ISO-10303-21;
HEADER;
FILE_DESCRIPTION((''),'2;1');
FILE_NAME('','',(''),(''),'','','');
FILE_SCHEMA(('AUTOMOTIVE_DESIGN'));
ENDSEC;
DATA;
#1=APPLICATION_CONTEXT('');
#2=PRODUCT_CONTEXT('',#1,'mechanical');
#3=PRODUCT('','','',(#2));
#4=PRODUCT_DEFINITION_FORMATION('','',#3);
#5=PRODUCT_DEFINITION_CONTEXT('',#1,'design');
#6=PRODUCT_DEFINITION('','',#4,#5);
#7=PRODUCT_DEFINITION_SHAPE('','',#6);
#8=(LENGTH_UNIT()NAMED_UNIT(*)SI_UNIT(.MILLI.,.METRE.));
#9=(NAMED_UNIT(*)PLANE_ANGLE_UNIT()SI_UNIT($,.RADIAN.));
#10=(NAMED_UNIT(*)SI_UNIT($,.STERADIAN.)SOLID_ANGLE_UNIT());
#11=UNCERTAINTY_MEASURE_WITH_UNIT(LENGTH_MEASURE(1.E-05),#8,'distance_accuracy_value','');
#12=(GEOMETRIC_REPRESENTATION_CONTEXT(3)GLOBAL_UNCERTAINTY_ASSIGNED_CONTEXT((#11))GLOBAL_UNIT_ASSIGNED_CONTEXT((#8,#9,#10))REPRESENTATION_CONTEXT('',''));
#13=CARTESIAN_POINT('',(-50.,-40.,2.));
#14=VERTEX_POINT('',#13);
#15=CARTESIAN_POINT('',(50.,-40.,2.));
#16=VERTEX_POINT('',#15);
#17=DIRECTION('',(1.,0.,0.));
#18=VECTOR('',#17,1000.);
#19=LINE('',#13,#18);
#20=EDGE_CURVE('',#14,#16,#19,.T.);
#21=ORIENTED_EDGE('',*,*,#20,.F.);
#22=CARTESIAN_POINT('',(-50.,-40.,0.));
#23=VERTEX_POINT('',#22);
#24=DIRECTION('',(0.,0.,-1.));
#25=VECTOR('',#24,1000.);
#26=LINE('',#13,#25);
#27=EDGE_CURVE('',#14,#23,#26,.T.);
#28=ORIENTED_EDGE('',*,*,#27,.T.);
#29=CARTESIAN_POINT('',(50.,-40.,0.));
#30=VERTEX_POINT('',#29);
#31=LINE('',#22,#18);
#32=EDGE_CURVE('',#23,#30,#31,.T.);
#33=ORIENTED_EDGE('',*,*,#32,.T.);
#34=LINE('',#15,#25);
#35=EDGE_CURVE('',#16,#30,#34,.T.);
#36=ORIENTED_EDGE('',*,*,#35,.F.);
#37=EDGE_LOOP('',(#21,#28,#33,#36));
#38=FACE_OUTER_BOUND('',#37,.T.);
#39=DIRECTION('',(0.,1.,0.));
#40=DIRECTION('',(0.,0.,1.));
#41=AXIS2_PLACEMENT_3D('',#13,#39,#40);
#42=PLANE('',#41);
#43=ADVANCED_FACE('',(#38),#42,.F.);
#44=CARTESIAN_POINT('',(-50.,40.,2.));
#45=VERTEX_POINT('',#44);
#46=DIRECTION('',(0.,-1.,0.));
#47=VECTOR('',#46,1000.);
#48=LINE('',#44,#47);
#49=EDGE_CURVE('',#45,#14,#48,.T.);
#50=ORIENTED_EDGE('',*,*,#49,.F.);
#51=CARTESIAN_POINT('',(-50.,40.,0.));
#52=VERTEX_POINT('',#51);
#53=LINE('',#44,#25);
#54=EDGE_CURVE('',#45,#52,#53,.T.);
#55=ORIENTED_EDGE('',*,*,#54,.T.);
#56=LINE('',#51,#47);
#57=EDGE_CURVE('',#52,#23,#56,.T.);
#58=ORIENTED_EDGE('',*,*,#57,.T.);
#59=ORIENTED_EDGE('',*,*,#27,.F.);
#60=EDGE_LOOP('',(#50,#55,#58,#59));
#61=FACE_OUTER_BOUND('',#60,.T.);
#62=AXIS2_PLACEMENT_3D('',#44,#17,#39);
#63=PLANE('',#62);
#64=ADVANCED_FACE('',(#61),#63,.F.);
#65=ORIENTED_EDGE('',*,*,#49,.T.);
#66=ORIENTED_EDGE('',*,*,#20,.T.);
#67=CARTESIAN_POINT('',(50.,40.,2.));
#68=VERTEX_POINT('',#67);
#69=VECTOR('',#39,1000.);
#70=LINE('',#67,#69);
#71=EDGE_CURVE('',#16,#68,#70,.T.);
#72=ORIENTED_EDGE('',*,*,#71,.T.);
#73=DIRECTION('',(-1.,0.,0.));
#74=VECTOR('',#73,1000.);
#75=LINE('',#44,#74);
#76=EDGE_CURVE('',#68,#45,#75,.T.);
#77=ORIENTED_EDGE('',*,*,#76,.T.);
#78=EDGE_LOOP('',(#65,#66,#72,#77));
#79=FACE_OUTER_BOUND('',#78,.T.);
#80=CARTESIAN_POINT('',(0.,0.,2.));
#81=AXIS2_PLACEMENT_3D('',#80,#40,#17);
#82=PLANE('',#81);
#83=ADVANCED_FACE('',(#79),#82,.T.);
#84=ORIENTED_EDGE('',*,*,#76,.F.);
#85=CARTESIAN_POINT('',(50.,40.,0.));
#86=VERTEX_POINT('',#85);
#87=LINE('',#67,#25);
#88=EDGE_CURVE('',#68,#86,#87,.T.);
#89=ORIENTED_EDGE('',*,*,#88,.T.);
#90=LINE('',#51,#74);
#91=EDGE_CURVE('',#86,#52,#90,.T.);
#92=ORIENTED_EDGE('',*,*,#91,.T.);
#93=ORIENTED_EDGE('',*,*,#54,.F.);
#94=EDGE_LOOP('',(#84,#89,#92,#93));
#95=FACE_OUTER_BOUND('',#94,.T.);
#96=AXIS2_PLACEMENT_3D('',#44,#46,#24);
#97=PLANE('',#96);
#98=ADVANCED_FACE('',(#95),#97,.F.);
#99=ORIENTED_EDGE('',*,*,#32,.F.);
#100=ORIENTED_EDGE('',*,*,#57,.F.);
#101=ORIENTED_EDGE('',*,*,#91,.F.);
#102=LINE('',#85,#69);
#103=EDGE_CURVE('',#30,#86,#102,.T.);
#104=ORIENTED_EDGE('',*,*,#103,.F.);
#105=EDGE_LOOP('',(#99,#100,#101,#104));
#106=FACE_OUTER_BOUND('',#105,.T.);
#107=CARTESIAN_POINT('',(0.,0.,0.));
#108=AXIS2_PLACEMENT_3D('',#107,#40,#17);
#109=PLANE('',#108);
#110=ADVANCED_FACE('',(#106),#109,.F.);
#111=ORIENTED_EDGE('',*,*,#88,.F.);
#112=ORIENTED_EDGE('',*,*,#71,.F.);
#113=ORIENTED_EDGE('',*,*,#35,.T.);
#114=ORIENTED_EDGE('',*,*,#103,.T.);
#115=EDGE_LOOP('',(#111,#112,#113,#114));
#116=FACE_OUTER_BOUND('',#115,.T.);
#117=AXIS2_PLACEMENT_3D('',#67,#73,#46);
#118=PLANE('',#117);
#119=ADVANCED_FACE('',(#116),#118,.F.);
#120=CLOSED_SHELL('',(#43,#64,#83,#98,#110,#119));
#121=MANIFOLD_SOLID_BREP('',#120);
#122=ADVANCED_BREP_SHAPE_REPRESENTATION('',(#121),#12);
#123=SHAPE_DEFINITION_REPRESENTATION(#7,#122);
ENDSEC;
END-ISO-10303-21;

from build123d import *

# Parameters (mm, degrees)
SKETCH1_W           = 100
SKETCH1_H           = 80
BOSS_EXTRUDE1_DEPTH = 2


with BuildPart() as part:
    # Sketch1 → Boss-Extrude1 (new body)
    with BuildSketch(Plane.XY):
        Rectangle(SKETCH1_W, SKETCH1_H)
    extrude(amount=BOSS_EXTRUDE1_DEPTH)


solid = part.part
